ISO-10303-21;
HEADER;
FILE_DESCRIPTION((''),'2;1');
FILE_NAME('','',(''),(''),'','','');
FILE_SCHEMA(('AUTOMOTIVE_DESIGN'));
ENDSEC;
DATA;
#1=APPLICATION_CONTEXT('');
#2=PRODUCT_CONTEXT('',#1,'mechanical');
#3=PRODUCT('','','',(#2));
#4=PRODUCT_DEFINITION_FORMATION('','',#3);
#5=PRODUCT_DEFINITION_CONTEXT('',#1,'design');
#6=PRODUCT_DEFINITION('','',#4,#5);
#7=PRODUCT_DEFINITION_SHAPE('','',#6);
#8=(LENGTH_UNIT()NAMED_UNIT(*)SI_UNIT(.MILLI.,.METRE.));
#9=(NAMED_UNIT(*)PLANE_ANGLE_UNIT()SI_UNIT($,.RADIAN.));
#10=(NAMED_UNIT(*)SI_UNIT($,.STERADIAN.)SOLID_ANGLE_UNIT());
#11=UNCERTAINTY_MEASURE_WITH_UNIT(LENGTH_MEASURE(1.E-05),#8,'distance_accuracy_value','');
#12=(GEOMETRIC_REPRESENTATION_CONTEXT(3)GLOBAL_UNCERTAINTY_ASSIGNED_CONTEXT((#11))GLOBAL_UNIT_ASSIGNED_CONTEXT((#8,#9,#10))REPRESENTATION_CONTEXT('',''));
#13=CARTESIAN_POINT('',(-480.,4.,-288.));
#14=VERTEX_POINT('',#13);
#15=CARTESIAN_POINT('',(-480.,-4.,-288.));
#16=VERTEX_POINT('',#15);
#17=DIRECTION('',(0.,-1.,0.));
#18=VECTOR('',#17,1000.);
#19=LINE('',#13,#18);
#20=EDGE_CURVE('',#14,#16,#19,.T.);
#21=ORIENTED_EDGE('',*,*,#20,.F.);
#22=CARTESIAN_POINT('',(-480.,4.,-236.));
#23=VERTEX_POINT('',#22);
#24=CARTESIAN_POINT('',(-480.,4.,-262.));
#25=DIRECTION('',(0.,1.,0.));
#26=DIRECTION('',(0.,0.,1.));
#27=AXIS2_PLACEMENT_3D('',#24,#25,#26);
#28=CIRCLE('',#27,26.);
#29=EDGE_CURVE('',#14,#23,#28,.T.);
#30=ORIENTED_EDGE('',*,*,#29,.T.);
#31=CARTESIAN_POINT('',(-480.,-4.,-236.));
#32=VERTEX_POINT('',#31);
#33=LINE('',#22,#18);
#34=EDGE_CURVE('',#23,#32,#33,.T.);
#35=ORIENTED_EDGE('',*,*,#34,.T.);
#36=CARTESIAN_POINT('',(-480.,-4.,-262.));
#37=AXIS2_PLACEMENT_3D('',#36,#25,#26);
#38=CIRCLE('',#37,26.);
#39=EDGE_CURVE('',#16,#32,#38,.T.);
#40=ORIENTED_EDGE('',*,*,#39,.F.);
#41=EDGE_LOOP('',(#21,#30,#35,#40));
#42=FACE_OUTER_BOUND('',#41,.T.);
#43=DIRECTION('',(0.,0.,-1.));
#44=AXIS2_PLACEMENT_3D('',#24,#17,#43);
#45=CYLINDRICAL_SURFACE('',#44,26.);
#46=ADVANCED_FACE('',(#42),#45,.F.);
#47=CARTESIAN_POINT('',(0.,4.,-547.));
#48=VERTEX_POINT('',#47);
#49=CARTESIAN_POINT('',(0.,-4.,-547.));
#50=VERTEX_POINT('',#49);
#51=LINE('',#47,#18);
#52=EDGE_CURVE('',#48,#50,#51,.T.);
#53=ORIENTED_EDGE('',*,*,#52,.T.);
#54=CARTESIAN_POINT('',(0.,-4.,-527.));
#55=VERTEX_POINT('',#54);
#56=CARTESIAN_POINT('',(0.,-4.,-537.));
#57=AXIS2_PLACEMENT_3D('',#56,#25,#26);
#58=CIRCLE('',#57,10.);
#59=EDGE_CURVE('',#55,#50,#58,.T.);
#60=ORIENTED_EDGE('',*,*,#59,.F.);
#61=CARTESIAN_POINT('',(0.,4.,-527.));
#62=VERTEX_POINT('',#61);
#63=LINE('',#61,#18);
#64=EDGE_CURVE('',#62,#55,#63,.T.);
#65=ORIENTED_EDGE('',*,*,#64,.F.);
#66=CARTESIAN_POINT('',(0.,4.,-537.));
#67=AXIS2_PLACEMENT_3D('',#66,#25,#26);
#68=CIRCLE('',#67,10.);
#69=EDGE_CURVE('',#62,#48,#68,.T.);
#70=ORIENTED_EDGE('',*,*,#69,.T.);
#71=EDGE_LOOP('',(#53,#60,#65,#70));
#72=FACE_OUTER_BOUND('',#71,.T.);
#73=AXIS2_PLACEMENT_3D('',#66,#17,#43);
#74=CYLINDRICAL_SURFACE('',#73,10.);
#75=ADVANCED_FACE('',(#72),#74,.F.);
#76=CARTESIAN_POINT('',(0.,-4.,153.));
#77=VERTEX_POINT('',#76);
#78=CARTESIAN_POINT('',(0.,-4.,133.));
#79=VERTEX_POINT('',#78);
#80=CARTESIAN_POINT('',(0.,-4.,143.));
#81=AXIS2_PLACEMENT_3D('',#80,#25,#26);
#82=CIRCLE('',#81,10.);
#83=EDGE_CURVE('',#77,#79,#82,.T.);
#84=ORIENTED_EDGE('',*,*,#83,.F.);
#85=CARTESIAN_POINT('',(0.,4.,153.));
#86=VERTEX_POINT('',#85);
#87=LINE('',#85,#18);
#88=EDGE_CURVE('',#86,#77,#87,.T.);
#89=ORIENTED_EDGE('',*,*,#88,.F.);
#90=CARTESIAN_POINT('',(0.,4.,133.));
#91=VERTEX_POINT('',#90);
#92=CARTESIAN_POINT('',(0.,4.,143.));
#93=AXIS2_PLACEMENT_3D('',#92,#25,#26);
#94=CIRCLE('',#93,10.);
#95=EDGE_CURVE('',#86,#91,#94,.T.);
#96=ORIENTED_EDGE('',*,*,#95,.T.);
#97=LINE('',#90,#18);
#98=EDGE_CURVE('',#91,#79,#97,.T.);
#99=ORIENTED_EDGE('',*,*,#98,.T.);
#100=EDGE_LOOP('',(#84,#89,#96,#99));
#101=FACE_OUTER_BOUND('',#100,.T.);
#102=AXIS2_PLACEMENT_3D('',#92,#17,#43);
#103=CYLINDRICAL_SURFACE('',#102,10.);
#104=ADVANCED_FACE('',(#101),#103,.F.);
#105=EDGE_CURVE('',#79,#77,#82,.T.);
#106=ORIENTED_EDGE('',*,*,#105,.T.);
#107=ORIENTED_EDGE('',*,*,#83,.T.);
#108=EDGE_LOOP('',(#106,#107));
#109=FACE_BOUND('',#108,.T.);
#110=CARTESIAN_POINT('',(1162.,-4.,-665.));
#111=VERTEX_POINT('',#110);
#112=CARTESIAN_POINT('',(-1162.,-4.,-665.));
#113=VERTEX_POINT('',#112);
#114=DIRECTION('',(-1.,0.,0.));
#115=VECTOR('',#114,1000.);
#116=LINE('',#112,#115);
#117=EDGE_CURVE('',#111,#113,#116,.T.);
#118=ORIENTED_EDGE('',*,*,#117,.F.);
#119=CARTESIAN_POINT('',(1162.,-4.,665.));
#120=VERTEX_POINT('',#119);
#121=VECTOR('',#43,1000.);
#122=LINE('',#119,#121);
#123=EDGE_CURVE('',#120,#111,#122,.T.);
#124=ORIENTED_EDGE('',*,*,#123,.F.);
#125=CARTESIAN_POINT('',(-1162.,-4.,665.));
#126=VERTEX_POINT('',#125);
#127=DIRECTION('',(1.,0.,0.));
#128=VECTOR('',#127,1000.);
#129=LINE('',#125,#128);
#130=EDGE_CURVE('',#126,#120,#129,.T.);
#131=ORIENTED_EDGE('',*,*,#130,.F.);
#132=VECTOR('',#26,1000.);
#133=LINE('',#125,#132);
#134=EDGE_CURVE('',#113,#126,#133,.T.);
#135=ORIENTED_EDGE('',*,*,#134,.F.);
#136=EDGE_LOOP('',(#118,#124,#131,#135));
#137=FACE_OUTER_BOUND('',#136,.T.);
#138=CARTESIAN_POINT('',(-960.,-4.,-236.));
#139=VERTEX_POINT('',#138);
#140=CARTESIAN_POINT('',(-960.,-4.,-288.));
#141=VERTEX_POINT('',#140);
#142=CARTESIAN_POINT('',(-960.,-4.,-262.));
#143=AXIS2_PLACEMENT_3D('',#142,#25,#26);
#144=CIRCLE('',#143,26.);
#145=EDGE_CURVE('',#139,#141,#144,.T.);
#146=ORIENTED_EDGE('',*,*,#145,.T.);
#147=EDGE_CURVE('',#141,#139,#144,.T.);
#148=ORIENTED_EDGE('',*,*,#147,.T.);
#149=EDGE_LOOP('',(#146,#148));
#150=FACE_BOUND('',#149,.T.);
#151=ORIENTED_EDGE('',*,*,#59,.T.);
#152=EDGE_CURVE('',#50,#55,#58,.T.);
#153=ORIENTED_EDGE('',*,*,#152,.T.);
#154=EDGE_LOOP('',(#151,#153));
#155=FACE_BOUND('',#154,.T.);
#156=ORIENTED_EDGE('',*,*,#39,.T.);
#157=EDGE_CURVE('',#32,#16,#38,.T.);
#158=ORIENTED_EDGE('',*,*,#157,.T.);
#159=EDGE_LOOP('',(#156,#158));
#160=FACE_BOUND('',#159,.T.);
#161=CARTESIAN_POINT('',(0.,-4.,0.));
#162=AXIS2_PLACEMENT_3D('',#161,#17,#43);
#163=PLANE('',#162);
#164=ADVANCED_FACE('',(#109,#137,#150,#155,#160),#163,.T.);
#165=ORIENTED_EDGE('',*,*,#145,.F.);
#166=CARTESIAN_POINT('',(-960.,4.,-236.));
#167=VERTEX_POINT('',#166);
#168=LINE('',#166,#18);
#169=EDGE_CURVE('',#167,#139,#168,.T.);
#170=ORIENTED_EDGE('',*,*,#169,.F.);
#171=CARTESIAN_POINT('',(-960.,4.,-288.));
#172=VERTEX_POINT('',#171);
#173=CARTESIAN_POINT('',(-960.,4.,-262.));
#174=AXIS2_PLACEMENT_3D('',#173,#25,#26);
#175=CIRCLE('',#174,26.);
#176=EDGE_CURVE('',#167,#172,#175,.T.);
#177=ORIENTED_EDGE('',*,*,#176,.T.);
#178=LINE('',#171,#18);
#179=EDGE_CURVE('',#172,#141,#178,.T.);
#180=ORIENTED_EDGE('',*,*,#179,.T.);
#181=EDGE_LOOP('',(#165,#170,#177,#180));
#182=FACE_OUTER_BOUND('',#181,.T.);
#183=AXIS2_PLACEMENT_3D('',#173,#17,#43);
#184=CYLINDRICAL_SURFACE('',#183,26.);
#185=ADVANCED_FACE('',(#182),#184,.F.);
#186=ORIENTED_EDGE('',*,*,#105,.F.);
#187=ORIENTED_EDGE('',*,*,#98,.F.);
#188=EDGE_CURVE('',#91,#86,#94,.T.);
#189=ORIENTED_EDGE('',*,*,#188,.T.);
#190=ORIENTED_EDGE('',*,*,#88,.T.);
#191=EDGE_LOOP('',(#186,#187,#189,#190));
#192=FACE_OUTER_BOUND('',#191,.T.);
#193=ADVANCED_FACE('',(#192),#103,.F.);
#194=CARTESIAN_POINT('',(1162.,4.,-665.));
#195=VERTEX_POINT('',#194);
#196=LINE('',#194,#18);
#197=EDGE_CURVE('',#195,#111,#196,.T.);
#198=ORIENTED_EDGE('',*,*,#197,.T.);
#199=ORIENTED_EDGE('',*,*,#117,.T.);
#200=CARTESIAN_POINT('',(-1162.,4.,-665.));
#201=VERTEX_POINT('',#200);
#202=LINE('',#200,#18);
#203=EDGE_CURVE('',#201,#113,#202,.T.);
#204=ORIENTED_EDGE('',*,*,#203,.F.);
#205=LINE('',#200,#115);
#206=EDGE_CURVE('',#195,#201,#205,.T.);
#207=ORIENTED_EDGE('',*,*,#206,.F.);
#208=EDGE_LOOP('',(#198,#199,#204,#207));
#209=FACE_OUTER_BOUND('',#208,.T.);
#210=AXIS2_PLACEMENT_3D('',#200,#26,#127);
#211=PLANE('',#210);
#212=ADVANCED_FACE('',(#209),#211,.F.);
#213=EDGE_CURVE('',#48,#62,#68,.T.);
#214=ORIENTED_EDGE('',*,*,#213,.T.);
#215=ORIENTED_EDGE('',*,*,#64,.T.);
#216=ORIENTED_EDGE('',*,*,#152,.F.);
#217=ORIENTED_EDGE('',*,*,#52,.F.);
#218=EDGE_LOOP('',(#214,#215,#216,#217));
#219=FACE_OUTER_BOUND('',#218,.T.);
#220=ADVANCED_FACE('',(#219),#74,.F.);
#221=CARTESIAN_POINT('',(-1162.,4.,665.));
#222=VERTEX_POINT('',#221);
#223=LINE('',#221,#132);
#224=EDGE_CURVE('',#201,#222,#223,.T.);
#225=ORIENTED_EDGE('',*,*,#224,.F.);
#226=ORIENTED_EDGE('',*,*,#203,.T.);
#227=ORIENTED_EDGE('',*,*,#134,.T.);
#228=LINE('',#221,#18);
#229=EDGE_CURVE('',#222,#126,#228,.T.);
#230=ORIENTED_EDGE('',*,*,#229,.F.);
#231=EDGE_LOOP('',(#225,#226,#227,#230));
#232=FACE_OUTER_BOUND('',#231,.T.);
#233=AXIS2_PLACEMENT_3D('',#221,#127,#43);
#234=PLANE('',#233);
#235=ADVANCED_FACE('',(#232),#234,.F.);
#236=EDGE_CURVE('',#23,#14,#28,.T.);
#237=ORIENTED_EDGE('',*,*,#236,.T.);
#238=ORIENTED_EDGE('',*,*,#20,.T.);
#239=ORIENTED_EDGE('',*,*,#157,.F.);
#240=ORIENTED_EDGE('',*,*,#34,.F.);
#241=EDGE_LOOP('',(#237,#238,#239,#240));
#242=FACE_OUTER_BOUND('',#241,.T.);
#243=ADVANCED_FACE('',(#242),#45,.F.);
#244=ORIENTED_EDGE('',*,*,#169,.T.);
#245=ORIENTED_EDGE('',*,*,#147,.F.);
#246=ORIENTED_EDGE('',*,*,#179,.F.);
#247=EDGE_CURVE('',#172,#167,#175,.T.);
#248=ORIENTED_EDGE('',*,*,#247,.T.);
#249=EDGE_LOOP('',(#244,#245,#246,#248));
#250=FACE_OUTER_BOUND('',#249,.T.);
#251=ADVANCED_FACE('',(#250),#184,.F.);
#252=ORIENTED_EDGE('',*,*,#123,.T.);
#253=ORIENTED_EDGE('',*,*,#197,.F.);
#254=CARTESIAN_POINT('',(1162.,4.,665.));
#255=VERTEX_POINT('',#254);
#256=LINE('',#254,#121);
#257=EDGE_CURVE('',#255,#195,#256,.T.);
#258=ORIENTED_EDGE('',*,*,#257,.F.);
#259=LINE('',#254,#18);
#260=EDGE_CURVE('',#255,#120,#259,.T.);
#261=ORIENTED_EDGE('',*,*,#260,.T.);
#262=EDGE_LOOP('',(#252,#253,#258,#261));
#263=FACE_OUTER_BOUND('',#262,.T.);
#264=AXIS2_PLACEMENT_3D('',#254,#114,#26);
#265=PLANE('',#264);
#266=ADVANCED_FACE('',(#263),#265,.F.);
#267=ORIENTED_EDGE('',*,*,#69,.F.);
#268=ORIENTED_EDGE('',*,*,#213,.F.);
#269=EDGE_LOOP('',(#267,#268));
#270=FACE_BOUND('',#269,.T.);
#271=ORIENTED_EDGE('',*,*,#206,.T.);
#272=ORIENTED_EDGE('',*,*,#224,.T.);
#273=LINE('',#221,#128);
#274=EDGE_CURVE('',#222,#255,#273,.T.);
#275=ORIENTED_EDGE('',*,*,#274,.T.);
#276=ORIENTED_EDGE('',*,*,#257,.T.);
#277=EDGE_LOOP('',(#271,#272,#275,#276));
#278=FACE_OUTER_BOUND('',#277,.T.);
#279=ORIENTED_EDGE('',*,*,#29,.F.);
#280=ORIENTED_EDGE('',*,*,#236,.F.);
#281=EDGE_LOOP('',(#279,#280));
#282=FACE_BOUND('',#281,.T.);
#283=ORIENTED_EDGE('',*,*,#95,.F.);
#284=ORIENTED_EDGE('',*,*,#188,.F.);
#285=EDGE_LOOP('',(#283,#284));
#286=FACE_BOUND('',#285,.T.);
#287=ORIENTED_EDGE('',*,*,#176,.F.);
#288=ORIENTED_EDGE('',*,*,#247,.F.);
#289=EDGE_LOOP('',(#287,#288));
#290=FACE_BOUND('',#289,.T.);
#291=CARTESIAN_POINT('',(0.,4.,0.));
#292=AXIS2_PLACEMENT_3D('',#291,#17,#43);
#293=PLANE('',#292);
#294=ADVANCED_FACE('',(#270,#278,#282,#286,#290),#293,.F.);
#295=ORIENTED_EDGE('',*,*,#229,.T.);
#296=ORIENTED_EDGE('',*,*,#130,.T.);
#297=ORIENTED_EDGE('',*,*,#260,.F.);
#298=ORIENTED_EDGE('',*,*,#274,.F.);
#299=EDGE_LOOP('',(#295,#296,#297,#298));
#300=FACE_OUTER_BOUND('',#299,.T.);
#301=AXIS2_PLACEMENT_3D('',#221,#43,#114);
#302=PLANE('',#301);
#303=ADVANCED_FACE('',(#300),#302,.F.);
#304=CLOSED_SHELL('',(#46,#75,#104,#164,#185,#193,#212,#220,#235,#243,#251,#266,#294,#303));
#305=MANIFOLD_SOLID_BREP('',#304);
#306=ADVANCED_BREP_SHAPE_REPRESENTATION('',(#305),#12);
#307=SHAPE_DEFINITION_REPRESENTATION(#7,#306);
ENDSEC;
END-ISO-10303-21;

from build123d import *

# Parameters (mm, degrees)
SKETCH_1_W      = 2324
SKETCH_1_H      = 1330
SKETCH_1_R      = 26
SKETCH_1_R_2    = 10
EXTRUDE_1_DEPTH = 4


with BuildPart() as part:
    # 草图1 → 凸台-拉伸1 (new, symmetric)
    with BuildSketch(Plane(origin=(0, 0, 0), x_dir=(1, 0, 0), z_dir=(0, 1, 0))):
        Rectangle(SKETCH_1_W, SKETCH_1_H)
        with Locations(Location((-480, 262, 0), (0, 0, 270))):
            Circle(SKETCH_1_R, mode=Mode.SUBTRACT)
        with Locations(Location((0, 537, 0), (0, 0, 270))):
            Circle(SKETCH_1_R_2, mode=Mode.SUBTRACT)
        with Locations(Location((0, -143, 0), (0, 0, 270))):
            Circle(SKETCH_1_R_2, mode=Mode.SUBTRACT)
        with Locations(Location((-960, 262, 0), (0, 0, 270))):
            Circle(SKETCH_1_R, mode=Mode.SUBTRACT)
    extrude(amount=EXTRUDE_1_DEPTH, both=True)


solid = part.part
